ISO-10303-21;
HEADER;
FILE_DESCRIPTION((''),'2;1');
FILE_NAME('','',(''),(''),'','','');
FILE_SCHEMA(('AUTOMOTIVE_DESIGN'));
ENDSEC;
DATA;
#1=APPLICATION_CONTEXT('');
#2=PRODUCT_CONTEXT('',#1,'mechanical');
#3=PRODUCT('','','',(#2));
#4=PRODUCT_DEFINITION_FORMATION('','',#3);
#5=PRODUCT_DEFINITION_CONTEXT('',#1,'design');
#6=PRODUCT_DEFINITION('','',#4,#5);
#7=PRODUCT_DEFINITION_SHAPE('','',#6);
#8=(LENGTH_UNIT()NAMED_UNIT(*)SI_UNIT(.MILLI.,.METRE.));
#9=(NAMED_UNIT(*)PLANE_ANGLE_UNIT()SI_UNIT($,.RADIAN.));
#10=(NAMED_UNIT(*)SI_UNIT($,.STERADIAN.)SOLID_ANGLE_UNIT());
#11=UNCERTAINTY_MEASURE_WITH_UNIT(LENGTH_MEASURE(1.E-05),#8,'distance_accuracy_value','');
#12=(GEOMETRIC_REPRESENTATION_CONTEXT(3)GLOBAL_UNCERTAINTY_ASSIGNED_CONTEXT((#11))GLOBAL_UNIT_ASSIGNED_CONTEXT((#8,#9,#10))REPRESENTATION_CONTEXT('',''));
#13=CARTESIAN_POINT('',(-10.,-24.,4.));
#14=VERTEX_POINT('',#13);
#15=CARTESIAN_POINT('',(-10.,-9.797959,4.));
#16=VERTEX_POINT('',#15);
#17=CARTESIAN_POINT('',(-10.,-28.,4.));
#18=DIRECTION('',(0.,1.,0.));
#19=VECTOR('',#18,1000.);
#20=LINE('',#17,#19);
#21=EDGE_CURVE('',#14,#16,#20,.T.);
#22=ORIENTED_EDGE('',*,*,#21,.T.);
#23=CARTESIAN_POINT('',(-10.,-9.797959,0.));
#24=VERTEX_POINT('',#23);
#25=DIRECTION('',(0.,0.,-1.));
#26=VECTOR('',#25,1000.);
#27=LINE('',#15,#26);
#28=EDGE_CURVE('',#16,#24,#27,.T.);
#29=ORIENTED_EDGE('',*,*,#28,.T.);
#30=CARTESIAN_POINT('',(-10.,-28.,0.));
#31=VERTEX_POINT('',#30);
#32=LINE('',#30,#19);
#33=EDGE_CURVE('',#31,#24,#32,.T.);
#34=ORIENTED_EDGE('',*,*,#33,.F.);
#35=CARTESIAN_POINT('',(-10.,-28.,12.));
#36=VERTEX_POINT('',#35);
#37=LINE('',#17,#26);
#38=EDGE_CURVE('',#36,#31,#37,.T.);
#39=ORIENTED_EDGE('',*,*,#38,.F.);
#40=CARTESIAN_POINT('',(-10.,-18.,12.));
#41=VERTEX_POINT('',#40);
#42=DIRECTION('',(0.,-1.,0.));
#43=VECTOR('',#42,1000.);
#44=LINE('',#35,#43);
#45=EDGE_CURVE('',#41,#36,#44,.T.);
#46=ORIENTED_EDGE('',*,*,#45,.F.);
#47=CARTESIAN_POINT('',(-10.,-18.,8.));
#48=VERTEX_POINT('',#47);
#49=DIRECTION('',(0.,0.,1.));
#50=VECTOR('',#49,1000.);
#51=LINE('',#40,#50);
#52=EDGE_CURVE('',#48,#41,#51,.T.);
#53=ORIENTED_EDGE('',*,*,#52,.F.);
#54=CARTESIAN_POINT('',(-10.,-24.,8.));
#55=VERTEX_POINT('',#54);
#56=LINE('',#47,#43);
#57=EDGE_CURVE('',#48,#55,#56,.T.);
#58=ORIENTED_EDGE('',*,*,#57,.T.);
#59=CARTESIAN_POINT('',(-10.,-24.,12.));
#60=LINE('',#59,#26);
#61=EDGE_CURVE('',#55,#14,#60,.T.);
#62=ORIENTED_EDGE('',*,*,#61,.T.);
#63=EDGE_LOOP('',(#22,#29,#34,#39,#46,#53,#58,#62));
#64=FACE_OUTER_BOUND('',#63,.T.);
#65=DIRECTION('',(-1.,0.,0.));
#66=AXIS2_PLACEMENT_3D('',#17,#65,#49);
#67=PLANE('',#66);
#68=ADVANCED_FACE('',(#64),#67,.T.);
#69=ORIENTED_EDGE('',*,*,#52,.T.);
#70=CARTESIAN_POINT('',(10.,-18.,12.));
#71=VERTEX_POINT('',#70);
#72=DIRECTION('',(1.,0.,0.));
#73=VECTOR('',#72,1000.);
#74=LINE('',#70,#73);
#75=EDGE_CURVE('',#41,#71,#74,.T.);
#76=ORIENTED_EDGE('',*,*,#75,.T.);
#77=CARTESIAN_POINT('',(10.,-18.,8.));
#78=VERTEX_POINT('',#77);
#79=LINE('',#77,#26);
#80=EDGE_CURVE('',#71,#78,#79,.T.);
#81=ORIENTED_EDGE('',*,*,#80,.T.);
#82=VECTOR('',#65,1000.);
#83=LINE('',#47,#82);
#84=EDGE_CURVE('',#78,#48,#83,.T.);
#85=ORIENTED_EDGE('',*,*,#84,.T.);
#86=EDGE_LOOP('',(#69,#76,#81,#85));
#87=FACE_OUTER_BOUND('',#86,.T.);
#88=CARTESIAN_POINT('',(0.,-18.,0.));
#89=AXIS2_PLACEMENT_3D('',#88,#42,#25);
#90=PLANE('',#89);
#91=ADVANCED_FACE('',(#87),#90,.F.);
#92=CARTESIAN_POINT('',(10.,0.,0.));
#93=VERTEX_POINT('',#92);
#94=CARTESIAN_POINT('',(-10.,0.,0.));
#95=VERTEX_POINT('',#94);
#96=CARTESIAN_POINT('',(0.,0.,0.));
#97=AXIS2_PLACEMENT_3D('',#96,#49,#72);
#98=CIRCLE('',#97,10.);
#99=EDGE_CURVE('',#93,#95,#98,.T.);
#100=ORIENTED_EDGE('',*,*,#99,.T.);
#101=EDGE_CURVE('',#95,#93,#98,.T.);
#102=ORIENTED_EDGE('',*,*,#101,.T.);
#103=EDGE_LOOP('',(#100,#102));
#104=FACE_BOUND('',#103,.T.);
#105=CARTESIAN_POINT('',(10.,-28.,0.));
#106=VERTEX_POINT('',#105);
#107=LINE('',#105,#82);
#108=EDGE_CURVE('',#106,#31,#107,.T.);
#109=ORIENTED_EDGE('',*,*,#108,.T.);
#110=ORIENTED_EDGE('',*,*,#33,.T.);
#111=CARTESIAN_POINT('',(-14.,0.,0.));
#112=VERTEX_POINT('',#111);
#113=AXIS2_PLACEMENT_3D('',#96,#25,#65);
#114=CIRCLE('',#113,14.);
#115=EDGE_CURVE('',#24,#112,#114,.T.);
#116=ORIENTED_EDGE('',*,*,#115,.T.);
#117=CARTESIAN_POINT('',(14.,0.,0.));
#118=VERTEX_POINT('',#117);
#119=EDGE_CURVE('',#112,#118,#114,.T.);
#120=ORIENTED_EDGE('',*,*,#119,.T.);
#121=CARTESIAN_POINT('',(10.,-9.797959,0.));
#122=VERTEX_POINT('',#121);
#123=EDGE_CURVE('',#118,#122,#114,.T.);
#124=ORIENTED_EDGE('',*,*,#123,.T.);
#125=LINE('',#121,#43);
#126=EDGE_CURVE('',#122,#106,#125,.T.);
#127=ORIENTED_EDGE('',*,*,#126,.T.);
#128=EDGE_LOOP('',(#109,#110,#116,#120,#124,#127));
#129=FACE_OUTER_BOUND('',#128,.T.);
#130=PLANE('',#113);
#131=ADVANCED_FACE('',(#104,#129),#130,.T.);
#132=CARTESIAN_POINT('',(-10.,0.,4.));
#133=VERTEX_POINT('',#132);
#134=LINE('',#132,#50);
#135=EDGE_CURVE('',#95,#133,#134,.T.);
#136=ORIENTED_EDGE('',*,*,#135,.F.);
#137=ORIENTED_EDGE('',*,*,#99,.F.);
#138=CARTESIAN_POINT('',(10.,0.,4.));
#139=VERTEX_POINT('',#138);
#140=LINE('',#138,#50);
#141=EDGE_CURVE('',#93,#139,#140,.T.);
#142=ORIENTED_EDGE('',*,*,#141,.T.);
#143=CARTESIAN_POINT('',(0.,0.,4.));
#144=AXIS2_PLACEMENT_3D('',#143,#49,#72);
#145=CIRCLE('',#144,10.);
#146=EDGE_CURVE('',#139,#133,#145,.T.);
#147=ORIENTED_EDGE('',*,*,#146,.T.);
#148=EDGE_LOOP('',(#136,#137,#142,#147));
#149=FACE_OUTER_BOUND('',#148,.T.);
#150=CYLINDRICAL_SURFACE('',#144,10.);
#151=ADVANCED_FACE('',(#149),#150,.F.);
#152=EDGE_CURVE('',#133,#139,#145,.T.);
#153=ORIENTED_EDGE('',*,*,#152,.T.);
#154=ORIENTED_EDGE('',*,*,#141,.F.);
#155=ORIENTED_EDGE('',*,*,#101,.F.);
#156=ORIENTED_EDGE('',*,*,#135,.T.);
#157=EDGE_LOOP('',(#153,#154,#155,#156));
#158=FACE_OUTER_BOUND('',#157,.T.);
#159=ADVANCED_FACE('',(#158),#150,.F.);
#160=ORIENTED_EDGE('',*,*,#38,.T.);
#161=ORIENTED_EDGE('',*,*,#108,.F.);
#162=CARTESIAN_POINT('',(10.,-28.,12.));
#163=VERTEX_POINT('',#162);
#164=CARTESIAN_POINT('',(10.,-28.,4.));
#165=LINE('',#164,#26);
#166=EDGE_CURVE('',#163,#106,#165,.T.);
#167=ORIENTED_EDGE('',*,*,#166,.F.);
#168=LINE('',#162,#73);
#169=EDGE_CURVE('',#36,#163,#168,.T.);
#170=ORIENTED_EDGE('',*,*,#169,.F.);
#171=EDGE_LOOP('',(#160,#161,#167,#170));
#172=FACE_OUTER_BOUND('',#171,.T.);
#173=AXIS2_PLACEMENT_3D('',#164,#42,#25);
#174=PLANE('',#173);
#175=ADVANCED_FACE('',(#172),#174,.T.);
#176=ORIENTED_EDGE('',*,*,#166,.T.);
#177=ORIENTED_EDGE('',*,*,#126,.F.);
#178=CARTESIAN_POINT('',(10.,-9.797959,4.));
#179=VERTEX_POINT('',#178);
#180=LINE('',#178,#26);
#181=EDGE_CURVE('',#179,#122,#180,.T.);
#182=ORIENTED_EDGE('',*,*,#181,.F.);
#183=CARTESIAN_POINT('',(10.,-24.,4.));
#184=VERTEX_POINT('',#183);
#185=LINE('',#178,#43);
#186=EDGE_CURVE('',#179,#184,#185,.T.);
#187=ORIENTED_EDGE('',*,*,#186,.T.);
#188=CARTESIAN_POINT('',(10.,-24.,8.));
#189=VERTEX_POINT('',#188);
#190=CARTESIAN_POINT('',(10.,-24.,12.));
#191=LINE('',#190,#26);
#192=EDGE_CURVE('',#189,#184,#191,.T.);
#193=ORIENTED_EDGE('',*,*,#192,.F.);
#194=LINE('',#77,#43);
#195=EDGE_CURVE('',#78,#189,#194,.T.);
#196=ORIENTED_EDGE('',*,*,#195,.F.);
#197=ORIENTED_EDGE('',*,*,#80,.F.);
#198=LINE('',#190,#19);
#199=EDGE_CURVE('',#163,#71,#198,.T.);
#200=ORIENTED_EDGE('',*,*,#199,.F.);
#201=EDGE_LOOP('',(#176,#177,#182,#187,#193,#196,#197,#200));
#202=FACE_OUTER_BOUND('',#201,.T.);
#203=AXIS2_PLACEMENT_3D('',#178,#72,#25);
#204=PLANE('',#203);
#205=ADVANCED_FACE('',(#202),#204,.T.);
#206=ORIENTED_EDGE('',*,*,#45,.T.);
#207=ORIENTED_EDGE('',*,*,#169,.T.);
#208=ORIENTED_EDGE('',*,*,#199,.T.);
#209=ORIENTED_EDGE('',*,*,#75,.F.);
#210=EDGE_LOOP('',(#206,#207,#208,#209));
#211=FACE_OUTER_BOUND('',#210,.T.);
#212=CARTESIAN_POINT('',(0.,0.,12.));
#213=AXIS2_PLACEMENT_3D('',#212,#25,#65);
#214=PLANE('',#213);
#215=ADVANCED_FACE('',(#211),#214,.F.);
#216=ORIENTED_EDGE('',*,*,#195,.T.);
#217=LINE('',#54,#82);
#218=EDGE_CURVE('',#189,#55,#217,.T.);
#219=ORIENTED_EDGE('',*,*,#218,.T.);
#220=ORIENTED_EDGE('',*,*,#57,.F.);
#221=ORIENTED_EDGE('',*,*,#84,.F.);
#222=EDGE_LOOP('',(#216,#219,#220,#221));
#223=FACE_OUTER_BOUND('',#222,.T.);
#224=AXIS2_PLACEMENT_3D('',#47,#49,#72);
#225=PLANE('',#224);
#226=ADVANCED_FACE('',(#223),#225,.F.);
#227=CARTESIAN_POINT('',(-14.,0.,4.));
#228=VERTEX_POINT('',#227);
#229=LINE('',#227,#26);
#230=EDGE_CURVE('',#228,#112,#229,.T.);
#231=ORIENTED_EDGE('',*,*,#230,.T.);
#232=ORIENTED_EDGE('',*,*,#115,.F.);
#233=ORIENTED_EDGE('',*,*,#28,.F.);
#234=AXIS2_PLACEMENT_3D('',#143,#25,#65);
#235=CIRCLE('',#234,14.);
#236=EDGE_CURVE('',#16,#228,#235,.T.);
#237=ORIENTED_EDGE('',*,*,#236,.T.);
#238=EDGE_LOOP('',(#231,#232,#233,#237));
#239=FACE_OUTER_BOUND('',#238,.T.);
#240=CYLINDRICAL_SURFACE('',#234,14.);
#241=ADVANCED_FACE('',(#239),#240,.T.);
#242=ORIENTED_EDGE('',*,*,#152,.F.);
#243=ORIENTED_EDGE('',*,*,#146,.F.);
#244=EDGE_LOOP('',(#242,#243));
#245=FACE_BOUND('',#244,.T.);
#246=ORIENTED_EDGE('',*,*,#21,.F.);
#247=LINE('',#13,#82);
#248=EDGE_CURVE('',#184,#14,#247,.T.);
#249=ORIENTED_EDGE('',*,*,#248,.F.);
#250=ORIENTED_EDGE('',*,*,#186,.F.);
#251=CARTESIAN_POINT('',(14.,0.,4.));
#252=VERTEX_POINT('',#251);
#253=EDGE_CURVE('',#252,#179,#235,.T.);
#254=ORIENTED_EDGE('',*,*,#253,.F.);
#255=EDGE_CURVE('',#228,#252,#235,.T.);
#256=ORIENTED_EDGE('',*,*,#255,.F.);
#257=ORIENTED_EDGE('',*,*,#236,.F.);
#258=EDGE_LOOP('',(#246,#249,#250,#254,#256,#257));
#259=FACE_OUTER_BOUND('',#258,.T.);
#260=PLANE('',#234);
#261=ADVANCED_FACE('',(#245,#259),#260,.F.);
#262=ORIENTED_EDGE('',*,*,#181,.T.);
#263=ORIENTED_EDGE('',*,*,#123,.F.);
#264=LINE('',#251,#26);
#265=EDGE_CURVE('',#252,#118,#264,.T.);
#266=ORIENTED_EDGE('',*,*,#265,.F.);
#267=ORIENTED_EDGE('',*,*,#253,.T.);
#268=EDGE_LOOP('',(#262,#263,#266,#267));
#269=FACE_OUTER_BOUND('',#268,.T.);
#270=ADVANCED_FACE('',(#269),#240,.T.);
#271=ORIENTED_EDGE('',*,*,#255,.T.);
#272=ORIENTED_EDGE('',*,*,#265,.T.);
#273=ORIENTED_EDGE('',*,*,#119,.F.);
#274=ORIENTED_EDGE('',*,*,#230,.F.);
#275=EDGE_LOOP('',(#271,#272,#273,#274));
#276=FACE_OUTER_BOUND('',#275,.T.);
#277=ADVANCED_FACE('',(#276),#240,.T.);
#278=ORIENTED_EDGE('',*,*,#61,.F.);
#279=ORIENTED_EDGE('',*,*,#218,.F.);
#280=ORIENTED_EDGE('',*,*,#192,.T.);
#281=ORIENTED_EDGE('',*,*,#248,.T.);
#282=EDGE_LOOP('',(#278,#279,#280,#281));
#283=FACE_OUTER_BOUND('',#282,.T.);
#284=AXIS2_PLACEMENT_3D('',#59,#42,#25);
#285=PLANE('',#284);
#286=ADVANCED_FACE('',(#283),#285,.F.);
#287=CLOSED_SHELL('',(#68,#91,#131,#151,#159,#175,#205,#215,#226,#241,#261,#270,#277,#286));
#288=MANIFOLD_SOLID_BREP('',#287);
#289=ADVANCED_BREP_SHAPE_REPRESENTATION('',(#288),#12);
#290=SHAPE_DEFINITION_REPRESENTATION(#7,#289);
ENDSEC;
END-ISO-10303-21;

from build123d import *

# Parameters (mm, degrees)
BOSS_EXTRUDE1_DEPTH        = 4
SKETCH2_W                  = 20
SKETCH2_H                  = 4
BOSS_EXTRUDE2_DEPTH        = 8
SKETCH3_W                  = 20
SKETCH3_H                  = 4
BOSS_EXTRUDE3_DEPTH        = 6
F_20_0_20_DIAMETER_HOLE1_D = 20


with BuildPart() as part:
    # Sketch1 → Boss-Extrude1 (new body)
    with BuildSketch(Plane(origin=(0, 0, 0), x_dir=(-1, 0, 0), z_dir=(0, 0, -1))):
        with BuildLine():
            Line((-10, -28), (10, -28))
            Line((10, -28), (10, -9.797958971))
            ThreePointArc((10, -9.797958971), (0, 14), (-10, -9.797958971))
            Line((-10, -9.797958971), (-10, -28))
        make_face()
    extrude(amount=-BOSS_EXTRUDE1_DEPTH)

    # Sketch2 → Boss-Extrude2 (add)
    with BuildSketch(Plane.XY.offset(4)):
        with Locations((0, -26)):
            Rectangle(SKETCH2_W, SKETCH2_H)
    extrude(amount=BOSS_EXTRUDE2_DEPTH)

    # Sketch3 → Boss-Extrude3 (add)
    with BuildSketch(Plane(origin=(0, -24, 0), x_dir=(-1, 0, 0), z_dir=(0, 1, 0))):
        with Locations((0, 10)):
            Rectangle(SKETCH3_W, SKETCH3_H)
    extrude(amount=BOSS_EXTRUDE3_DEPTH)

    # Ø20.0 (20) Diameter Hole1 (through all)
    with Locations(Plane.XY.offset(4)):
        with Locations((0, 0)):
            Hole(F_20_0_20_DIAMETER_HOLE1_D / 2)


solid = part.part
